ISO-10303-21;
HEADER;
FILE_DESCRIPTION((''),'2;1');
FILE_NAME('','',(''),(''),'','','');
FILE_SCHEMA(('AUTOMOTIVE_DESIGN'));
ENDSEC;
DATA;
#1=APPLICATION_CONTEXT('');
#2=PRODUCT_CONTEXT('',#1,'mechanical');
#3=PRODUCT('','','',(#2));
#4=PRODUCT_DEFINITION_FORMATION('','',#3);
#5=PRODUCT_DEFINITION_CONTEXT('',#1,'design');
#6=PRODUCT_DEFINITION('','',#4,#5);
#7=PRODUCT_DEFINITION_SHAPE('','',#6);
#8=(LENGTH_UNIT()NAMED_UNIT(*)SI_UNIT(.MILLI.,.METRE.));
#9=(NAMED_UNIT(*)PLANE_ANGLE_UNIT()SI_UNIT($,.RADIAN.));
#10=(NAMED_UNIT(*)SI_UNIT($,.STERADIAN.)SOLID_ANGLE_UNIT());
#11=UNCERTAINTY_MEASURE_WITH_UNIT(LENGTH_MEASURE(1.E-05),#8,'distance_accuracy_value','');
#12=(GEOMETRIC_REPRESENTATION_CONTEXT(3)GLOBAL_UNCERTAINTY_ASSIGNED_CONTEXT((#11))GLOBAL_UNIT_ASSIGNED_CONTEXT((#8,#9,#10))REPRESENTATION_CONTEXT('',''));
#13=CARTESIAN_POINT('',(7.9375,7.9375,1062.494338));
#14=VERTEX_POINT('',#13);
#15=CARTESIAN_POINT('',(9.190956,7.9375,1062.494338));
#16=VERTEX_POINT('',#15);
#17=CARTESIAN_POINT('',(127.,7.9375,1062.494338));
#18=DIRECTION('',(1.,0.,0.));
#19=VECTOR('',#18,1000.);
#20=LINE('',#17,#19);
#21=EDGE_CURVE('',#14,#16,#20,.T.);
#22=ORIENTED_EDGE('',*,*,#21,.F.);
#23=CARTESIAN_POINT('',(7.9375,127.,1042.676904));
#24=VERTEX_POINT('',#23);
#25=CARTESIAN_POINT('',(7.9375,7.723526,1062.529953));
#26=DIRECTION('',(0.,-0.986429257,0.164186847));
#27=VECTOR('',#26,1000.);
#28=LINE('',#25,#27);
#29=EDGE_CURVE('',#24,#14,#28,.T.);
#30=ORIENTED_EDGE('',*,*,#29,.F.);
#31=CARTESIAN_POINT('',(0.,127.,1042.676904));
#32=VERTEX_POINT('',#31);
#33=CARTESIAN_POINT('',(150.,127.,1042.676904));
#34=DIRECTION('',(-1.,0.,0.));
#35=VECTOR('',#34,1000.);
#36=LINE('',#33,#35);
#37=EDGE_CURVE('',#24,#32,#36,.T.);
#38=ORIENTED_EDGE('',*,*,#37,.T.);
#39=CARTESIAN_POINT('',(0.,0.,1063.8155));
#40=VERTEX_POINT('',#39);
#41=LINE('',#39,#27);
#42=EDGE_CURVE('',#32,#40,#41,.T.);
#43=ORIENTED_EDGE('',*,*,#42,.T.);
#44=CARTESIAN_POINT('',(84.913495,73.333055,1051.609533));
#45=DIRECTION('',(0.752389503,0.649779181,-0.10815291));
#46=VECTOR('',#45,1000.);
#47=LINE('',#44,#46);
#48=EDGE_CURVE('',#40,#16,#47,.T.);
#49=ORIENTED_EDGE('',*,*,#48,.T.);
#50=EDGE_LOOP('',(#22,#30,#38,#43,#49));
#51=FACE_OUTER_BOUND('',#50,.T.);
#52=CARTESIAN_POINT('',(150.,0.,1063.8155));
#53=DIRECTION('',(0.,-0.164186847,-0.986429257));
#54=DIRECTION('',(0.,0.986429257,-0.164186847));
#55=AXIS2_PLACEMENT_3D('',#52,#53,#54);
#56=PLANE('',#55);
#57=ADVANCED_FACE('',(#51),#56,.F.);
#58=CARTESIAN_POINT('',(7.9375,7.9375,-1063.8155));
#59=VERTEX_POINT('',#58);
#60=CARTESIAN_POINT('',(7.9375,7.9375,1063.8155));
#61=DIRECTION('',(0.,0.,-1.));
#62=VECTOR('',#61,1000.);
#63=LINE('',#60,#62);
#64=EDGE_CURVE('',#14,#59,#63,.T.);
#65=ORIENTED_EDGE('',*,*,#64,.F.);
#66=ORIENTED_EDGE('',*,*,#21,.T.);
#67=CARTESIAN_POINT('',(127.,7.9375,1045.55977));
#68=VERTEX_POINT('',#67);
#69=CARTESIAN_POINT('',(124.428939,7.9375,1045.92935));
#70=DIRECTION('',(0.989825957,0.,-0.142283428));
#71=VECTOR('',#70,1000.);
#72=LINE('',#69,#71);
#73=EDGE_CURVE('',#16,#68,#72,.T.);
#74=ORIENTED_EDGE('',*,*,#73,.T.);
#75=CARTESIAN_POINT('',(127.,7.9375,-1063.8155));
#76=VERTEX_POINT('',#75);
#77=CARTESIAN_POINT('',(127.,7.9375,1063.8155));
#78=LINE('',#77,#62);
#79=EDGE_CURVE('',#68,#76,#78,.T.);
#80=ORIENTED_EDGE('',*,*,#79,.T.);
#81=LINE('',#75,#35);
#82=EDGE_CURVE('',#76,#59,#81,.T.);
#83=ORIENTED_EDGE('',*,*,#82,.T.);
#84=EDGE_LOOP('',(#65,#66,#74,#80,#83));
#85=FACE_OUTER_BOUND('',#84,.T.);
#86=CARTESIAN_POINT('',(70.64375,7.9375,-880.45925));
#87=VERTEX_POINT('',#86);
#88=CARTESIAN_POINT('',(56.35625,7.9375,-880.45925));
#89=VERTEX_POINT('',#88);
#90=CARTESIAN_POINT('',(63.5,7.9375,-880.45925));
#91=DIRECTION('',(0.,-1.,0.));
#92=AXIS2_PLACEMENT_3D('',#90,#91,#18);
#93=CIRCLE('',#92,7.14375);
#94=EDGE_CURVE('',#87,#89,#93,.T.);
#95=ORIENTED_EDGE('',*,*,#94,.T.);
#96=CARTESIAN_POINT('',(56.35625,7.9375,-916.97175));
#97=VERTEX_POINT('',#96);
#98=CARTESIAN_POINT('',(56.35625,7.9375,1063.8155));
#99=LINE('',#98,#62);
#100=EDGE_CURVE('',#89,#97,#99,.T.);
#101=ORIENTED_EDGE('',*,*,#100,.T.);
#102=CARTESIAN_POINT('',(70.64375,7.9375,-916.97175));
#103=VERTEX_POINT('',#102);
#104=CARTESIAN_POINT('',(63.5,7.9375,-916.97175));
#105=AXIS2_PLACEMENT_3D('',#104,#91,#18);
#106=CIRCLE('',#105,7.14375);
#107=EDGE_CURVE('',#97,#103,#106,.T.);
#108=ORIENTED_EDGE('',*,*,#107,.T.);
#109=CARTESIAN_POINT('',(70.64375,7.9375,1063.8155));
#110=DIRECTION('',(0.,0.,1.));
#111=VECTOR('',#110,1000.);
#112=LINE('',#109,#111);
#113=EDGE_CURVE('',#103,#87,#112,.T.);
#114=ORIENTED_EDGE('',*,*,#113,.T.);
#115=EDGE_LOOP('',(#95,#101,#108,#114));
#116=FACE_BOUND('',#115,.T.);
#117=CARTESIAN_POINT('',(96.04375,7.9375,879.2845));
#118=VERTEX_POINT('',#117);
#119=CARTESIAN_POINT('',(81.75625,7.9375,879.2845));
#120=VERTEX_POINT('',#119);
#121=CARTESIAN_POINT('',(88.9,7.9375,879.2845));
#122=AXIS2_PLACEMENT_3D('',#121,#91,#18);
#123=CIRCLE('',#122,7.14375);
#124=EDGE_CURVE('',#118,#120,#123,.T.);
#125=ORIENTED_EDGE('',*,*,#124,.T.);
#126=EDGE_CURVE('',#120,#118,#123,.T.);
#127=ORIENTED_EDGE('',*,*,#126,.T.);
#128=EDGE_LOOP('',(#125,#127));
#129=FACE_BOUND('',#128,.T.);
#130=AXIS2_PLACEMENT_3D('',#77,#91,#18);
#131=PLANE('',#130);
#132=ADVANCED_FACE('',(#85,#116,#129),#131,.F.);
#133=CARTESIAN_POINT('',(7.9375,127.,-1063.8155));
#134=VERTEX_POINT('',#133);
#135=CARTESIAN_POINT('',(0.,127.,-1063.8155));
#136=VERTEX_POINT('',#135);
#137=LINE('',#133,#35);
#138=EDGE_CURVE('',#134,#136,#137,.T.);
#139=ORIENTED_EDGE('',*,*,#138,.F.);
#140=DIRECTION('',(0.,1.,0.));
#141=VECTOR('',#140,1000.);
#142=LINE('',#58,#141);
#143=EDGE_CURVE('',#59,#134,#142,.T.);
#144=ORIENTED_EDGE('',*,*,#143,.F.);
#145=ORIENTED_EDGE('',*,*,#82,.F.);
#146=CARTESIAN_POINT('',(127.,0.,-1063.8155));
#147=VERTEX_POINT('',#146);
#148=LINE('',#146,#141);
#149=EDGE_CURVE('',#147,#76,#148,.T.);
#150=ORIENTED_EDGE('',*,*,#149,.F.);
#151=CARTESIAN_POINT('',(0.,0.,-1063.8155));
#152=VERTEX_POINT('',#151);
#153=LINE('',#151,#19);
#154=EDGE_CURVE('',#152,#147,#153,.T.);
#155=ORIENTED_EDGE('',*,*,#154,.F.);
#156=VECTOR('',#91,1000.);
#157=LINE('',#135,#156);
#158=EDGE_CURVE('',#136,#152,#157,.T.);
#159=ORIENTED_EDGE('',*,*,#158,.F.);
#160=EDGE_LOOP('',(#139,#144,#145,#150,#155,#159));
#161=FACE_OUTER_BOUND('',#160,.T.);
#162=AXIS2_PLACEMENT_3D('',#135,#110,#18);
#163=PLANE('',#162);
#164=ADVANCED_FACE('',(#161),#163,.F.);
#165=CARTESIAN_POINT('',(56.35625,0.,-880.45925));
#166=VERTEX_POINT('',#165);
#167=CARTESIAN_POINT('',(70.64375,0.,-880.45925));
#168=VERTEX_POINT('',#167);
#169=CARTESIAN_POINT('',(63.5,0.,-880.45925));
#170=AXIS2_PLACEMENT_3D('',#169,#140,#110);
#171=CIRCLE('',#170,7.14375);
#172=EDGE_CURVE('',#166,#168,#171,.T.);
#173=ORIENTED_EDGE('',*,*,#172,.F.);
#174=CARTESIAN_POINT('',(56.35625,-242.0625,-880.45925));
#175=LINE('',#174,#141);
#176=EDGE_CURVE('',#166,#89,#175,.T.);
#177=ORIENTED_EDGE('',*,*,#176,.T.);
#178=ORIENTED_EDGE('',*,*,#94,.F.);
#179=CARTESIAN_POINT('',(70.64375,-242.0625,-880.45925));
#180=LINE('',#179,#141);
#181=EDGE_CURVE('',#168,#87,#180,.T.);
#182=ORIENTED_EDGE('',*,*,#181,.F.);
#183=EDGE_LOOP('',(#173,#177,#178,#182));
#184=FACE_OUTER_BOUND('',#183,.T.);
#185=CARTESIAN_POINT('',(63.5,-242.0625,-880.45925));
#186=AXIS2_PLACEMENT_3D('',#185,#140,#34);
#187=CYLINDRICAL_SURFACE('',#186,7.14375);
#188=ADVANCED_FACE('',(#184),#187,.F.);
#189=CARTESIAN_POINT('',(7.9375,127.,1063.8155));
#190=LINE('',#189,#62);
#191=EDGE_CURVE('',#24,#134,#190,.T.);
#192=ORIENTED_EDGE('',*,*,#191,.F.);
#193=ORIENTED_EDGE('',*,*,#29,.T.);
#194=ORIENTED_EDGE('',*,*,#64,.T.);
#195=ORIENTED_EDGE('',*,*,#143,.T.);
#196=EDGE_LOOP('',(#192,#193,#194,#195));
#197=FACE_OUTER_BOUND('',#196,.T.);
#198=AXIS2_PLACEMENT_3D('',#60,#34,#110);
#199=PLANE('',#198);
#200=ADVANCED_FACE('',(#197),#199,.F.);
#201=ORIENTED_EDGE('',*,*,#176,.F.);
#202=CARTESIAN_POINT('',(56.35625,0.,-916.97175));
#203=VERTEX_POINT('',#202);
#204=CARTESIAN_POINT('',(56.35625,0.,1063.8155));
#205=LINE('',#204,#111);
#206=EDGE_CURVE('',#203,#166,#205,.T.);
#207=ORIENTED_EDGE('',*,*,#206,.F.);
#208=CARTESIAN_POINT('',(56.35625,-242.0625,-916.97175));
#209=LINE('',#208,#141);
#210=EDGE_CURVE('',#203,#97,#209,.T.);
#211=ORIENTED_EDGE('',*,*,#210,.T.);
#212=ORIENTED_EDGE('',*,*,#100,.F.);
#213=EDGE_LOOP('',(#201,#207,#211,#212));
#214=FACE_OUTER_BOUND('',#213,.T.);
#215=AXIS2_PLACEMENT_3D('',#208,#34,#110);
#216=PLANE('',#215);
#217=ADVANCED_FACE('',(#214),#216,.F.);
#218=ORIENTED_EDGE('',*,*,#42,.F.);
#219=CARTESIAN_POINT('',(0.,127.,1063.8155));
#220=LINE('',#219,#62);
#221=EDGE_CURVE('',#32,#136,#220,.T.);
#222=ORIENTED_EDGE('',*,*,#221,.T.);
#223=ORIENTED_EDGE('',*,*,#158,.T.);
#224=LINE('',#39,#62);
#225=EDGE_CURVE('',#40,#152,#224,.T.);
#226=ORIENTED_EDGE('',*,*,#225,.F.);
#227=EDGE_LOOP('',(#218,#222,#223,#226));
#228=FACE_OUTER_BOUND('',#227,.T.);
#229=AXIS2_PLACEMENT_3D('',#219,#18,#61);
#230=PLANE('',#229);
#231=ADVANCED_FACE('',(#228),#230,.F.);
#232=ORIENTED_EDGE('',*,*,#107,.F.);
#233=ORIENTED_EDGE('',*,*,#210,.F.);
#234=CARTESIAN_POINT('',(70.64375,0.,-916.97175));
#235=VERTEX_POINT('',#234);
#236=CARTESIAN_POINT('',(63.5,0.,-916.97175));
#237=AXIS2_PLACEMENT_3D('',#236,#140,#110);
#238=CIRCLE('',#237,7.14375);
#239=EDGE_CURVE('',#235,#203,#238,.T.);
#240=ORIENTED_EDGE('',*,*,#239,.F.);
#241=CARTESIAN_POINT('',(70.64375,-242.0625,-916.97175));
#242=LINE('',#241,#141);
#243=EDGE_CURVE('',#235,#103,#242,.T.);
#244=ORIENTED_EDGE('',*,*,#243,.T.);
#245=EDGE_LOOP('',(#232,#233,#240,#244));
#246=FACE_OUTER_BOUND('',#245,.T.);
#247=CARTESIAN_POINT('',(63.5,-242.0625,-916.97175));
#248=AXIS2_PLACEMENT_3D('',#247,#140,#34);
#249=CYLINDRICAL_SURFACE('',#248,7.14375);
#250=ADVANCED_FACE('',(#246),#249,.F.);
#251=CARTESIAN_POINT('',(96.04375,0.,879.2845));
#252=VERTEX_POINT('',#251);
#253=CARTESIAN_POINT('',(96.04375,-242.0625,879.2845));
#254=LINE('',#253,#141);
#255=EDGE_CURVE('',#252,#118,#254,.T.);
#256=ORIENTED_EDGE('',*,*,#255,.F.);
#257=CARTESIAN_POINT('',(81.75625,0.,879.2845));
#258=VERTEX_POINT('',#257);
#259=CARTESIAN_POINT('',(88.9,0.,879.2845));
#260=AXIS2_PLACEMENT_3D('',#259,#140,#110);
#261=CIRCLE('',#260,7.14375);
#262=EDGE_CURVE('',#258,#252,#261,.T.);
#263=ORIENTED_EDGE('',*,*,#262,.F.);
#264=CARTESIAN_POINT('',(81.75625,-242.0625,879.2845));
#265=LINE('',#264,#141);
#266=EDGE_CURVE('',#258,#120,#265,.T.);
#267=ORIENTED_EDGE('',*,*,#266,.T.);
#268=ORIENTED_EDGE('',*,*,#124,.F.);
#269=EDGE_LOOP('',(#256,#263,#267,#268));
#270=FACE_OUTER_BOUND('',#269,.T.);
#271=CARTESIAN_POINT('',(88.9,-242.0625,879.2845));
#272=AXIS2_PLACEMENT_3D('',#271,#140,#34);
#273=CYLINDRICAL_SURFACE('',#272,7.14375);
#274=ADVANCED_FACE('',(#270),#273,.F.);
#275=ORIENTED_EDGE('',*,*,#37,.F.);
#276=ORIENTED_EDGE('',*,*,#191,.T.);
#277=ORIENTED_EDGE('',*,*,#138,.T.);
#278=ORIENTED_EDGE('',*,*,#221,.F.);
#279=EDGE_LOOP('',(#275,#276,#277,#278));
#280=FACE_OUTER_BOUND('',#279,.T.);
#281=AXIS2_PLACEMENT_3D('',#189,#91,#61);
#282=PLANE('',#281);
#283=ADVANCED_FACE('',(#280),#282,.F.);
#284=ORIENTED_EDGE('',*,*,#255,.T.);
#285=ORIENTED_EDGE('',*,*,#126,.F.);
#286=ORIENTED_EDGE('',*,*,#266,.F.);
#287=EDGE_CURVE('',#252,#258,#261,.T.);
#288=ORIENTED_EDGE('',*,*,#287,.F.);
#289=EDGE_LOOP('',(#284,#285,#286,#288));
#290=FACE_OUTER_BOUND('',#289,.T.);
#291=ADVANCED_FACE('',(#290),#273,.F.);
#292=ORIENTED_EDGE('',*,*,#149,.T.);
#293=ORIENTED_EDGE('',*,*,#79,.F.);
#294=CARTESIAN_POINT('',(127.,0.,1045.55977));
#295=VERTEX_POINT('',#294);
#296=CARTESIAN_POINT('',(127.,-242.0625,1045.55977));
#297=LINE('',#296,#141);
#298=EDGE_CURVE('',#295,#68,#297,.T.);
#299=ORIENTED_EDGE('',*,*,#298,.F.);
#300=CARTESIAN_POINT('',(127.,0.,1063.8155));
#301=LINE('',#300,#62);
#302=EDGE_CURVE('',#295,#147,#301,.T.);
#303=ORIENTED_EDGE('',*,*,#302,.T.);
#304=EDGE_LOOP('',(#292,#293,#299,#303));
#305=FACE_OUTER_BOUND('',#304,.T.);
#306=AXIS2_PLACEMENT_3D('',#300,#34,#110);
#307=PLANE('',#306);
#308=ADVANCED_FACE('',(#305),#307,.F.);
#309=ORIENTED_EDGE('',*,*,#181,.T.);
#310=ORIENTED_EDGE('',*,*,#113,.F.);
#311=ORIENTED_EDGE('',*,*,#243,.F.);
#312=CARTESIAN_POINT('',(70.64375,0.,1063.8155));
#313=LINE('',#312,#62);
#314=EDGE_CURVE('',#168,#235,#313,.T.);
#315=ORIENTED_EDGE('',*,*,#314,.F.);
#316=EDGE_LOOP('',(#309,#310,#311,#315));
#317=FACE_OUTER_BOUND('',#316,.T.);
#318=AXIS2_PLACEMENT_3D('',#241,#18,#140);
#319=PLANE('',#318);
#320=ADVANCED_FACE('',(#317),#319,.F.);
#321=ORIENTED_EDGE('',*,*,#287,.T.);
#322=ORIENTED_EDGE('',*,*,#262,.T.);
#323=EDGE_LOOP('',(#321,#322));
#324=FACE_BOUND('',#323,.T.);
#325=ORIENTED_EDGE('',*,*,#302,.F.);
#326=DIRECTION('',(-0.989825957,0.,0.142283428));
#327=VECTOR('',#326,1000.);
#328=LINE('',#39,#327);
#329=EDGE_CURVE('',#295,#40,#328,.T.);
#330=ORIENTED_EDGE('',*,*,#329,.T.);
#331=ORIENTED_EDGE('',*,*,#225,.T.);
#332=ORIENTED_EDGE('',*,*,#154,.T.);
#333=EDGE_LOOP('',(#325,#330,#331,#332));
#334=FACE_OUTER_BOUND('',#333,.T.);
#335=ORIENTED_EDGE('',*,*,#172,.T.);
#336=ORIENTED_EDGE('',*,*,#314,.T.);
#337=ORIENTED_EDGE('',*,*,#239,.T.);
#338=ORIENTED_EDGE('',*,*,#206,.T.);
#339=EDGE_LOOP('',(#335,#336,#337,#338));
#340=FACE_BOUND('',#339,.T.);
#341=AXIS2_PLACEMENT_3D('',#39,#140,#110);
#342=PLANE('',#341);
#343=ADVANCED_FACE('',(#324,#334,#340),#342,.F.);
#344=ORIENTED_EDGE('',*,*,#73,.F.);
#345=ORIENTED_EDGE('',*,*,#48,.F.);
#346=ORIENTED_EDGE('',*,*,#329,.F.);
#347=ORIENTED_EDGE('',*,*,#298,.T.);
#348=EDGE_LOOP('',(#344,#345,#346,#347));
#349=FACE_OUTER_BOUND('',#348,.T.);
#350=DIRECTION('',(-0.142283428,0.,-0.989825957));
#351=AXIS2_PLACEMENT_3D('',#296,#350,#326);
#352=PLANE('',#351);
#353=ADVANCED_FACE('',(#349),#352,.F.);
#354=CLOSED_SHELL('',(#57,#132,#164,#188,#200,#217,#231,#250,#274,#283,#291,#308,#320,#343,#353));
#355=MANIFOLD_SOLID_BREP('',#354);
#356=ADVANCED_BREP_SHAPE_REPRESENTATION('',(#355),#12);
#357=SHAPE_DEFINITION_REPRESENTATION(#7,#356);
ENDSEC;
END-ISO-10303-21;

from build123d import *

# Parameters (mm, degrees)
BOSS_EXTRUDE1_DEPTH = 1063.8155
CUT_EXTRUDE1_DEPTH  = 150
SKETCH3_R           = 7.14375
CUT_EXTRUDE2_DEPTH  = 250


with BuildPart() as part:
    # Sketch1 → Boss-Extrude1 (new, symmetric)
    with BuildSketch(Plane.XY):
        Polygon((0, 127), (0, 0), (127, 0), (127, 7.9375), (7.9375, 7.9375), (7.9375, 127), align=None)
    extrude(amount=BOSS_EXTRUDE1_DEPTH, both=True)

    # Sketch2 → Cut-Extrude1 (cut)
    with BuildSketch(Plane.ZY):
        Polygon((1063.8155, 0), (1042.676904036, 127), (1063.8155, 127), align=None)
    extrude(amount=-CUT_EXTRUDE1_DEPTH, mode=Mode.SUBTRACT)

    # Sketch3 → Cut-Extrude2 (cut, symmetric)
    with BuildSketch(Plane(origin=(0, 7.9375, 0), x_dir=(1, 0, 0), z_dir=(0, 1, 0))):
        with Locations(Location((88.9, -879.2845, 0), (0, 0, 270))):
            Circle(SKETCH3_R)
        Polygon((0, -1063.8155), (127, -1063.8155), (127, -1045.559770079), align=None)
        with BuildLine():
            Line((70.64375, 916.97175), (70.64375, 880.45925))
            ThreePointArc((70.64375, 880.45925), (63.5, 873.3155), (56.35625, 880.45925))
            Line((56.35625, 880.45925), (56.35625, 916.97175))
            ThreePointArc((56.35625, 916.97175), (63.5, 924.1155), (70.64375, 916.97175))
        make_face()
    extrude(amount=CUT_EXTRUDE2_DEPTH, both=True, mode=Mode.SUBTRACT)


solid = part.part
